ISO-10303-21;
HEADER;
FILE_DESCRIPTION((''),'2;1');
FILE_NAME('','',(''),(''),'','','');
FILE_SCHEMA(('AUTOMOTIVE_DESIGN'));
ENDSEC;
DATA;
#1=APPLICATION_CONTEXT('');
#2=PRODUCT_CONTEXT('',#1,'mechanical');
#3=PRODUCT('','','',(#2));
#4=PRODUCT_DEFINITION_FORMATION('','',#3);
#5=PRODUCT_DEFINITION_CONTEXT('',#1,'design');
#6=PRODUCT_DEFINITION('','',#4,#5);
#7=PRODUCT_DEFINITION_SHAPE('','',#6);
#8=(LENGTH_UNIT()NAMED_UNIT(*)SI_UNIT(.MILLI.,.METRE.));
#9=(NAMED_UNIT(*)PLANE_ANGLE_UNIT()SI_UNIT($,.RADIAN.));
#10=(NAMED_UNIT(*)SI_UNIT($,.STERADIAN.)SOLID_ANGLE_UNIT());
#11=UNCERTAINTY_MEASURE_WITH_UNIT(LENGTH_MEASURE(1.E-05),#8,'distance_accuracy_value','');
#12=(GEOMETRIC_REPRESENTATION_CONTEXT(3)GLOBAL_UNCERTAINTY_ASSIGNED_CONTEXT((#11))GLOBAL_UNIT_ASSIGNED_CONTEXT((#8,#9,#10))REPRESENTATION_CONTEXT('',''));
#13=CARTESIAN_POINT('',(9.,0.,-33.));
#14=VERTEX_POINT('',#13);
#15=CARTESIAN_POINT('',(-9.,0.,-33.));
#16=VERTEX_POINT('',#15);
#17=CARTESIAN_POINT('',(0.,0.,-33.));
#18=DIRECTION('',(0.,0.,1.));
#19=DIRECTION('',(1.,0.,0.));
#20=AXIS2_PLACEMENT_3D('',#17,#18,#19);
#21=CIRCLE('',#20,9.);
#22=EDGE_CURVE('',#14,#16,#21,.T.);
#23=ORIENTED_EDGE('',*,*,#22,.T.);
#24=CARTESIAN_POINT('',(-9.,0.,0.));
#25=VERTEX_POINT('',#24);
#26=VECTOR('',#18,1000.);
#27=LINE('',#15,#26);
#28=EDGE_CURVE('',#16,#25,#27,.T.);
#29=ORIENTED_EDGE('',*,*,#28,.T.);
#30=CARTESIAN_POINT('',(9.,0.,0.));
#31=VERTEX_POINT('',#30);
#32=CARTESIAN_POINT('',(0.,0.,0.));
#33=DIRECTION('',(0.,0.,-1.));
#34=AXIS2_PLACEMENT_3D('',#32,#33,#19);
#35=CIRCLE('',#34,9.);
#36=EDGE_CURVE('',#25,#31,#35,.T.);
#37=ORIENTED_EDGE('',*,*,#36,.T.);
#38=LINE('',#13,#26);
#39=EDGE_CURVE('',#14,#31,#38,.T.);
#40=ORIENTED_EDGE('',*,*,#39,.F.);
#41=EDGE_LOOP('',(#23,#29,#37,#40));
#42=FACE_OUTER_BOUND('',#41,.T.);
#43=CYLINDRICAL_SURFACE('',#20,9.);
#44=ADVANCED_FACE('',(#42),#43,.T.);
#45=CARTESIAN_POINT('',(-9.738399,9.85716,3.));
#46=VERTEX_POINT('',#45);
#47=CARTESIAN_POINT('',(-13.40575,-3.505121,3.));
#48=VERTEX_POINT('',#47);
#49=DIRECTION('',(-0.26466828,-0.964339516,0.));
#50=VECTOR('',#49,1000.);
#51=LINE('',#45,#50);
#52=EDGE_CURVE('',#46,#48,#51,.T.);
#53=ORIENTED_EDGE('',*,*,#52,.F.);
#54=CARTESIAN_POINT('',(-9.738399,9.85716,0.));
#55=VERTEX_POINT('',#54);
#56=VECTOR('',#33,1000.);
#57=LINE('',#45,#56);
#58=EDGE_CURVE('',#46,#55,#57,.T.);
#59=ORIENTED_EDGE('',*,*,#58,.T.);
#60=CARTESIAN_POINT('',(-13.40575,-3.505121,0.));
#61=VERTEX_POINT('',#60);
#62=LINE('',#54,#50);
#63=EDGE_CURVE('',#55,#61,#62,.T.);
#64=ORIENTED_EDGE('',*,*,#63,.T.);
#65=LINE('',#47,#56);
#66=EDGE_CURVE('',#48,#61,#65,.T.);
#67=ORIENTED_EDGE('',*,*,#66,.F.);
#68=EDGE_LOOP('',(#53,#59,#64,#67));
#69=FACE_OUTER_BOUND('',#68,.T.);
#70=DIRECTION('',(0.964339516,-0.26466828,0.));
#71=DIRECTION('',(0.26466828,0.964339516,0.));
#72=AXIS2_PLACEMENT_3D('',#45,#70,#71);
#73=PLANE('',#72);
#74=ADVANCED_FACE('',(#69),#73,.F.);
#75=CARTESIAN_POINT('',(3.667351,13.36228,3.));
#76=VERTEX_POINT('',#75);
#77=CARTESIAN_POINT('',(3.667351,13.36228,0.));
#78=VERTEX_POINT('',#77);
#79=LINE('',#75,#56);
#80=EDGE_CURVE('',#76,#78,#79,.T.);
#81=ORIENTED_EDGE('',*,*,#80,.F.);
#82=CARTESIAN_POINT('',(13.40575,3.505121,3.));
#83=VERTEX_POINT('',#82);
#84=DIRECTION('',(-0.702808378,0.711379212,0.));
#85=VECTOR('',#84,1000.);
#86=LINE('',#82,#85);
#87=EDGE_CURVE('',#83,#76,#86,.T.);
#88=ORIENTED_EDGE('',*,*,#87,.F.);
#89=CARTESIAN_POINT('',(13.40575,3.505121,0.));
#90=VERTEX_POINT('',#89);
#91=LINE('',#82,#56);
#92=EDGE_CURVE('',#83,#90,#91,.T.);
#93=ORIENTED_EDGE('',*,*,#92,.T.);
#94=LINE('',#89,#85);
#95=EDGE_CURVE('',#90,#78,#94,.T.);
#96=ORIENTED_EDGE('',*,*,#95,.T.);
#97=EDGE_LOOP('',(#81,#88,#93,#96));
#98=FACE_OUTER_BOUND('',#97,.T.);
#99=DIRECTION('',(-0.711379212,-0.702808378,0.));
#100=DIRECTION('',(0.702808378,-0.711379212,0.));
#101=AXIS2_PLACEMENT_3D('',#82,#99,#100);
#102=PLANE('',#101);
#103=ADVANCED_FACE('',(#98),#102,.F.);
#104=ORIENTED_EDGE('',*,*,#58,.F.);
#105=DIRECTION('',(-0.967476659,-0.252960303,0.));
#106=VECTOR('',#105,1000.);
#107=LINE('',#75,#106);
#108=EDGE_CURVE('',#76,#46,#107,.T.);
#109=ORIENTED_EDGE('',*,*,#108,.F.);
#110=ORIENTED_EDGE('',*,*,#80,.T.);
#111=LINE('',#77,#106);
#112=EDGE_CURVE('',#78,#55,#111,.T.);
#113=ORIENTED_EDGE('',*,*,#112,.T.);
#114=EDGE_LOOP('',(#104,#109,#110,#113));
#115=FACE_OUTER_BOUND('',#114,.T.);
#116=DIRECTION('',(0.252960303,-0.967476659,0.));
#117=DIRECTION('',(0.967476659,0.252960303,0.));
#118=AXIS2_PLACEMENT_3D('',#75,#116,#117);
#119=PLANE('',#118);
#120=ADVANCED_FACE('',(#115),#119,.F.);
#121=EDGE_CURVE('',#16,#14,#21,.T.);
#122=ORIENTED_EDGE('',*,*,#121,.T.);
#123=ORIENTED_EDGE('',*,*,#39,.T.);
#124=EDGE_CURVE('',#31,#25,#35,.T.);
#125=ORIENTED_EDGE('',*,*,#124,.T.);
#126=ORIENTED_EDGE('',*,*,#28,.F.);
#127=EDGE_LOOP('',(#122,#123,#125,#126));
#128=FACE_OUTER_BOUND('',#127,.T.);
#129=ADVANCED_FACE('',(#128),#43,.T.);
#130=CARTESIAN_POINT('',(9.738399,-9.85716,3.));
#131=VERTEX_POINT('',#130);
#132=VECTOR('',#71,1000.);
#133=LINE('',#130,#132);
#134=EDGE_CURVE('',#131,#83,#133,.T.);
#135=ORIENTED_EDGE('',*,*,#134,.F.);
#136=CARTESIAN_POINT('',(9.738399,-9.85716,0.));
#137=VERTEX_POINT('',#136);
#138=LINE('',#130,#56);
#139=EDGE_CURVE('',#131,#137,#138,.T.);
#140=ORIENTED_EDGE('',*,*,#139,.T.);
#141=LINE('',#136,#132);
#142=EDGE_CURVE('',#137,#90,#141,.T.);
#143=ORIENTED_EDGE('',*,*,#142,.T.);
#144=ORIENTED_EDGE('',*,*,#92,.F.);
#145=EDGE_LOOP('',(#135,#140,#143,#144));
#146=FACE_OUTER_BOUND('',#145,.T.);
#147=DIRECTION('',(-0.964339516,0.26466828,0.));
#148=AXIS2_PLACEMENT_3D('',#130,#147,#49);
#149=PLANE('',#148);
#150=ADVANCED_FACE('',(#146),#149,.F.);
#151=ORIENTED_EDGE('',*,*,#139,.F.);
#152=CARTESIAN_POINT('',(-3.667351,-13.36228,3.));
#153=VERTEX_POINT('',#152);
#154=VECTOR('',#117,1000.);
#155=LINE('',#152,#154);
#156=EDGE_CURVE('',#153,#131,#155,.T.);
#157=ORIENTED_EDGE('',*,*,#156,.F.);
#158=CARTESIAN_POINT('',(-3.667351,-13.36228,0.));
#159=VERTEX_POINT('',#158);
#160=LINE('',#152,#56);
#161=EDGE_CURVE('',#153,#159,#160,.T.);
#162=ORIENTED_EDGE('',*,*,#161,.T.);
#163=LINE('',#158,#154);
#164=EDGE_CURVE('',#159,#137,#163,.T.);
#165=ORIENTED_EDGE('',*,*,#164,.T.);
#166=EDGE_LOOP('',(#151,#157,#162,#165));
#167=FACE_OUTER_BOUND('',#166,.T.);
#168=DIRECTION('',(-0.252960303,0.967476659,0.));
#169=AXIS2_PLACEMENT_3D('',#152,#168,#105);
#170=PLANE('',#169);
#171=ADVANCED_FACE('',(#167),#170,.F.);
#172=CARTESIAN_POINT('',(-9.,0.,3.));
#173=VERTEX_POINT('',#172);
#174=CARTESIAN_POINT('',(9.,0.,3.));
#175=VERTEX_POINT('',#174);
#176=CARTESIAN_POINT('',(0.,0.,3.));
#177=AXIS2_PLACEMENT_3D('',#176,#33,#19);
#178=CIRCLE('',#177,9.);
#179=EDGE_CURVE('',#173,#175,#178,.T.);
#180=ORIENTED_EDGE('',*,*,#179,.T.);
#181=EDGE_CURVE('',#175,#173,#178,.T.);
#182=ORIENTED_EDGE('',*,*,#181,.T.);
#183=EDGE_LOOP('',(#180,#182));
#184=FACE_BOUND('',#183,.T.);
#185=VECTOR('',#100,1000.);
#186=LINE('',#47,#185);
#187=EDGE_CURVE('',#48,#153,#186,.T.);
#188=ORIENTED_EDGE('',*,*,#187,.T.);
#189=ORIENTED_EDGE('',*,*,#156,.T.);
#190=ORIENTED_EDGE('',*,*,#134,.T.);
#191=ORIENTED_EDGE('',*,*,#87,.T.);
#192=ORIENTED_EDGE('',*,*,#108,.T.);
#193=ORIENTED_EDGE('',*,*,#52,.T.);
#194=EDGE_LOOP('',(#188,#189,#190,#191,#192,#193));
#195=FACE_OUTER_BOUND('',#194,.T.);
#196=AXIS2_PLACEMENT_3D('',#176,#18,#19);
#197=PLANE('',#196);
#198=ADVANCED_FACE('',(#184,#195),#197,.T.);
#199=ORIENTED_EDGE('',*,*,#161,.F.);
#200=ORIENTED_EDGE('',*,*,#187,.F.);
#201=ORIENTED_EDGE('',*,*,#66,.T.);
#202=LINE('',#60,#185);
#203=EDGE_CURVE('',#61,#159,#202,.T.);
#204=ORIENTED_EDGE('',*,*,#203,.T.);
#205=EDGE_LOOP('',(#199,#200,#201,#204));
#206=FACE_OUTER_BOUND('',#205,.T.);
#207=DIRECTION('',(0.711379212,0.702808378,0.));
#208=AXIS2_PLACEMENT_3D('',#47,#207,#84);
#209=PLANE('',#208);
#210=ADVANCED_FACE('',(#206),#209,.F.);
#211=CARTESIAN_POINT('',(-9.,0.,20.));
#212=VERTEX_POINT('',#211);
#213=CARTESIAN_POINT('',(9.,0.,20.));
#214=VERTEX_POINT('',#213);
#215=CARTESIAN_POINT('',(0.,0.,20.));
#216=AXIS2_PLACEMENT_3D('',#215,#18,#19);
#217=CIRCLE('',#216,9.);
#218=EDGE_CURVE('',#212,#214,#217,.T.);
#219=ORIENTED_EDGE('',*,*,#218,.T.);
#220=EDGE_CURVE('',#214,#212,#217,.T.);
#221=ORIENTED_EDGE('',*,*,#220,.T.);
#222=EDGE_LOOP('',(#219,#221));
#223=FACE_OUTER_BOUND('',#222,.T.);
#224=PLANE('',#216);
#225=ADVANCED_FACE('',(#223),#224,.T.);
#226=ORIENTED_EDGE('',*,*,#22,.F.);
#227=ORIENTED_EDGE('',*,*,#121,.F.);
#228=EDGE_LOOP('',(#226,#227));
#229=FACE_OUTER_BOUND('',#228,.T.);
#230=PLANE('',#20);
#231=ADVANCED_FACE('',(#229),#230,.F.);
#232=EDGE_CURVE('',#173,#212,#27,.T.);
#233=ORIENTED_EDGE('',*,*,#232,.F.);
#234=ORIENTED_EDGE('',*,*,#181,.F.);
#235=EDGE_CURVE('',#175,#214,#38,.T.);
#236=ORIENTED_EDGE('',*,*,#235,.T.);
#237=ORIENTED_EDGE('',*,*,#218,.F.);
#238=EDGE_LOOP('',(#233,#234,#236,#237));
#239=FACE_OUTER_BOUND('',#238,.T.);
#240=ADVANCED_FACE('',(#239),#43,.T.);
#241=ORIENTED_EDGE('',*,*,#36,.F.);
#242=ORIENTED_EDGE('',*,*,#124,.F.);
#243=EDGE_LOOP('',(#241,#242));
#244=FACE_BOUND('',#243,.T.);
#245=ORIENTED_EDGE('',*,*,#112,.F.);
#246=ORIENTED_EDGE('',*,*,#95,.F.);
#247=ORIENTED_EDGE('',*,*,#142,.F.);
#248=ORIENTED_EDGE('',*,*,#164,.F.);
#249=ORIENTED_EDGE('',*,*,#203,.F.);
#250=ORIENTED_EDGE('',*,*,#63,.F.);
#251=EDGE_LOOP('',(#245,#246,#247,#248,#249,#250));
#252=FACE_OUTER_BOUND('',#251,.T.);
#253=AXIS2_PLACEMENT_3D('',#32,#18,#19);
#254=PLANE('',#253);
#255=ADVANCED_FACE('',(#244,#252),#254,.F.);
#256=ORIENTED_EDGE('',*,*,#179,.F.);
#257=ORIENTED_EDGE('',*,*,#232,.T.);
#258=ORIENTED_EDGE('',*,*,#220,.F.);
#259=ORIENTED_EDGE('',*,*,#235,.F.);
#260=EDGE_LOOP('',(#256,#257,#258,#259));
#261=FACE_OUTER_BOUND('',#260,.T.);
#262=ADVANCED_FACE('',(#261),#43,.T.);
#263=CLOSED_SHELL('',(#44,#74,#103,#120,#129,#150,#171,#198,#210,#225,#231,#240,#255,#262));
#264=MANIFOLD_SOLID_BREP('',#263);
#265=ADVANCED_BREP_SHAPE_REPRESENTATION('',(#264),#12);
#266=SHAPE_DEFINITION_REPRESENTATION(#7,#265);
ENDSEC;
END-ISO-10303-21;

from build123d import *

# Parameters (mm, degrees)
BOSS_EXTRUDE1_DEPTH      = 20
BOSS_EXTRUDE1_DEPTH_BACK = 33
SKETCH1_R                = 9
BOSS_EXTRUDE2_DEPTH      = 3


with BuildPart() as part:
    # Sketch1 → Boss-Extrude1 (new, two sides: drawn at the far end of the back side and taken through both)
    with BuildSketch(Plane.XY.offset(-BOSS_EXTRUDE1_DEPTH_BACK)):
        Circle(SKETCH1_R)
    extrude(amount=BOSS_EXTRUDE1_DEPTH + BOSS_EXTRUDE1_DEPTH_BACK)

    # Sketch2 → Boss-Extrude2 (add)
    with BuildSketch(Plane.XY):
        Polygon((9.738398553, -9.857159511), (13.405749822, 3.505120784), (3.667351269, 13.362280294), (-9.738398553, 9.857159511), (-13.405749822, -3.505120784), (-3.667351269, -13.362280294), align=None)
    extrude(amount=BOSS_EXTRUDE2_DEPTH)


solid = part.part
